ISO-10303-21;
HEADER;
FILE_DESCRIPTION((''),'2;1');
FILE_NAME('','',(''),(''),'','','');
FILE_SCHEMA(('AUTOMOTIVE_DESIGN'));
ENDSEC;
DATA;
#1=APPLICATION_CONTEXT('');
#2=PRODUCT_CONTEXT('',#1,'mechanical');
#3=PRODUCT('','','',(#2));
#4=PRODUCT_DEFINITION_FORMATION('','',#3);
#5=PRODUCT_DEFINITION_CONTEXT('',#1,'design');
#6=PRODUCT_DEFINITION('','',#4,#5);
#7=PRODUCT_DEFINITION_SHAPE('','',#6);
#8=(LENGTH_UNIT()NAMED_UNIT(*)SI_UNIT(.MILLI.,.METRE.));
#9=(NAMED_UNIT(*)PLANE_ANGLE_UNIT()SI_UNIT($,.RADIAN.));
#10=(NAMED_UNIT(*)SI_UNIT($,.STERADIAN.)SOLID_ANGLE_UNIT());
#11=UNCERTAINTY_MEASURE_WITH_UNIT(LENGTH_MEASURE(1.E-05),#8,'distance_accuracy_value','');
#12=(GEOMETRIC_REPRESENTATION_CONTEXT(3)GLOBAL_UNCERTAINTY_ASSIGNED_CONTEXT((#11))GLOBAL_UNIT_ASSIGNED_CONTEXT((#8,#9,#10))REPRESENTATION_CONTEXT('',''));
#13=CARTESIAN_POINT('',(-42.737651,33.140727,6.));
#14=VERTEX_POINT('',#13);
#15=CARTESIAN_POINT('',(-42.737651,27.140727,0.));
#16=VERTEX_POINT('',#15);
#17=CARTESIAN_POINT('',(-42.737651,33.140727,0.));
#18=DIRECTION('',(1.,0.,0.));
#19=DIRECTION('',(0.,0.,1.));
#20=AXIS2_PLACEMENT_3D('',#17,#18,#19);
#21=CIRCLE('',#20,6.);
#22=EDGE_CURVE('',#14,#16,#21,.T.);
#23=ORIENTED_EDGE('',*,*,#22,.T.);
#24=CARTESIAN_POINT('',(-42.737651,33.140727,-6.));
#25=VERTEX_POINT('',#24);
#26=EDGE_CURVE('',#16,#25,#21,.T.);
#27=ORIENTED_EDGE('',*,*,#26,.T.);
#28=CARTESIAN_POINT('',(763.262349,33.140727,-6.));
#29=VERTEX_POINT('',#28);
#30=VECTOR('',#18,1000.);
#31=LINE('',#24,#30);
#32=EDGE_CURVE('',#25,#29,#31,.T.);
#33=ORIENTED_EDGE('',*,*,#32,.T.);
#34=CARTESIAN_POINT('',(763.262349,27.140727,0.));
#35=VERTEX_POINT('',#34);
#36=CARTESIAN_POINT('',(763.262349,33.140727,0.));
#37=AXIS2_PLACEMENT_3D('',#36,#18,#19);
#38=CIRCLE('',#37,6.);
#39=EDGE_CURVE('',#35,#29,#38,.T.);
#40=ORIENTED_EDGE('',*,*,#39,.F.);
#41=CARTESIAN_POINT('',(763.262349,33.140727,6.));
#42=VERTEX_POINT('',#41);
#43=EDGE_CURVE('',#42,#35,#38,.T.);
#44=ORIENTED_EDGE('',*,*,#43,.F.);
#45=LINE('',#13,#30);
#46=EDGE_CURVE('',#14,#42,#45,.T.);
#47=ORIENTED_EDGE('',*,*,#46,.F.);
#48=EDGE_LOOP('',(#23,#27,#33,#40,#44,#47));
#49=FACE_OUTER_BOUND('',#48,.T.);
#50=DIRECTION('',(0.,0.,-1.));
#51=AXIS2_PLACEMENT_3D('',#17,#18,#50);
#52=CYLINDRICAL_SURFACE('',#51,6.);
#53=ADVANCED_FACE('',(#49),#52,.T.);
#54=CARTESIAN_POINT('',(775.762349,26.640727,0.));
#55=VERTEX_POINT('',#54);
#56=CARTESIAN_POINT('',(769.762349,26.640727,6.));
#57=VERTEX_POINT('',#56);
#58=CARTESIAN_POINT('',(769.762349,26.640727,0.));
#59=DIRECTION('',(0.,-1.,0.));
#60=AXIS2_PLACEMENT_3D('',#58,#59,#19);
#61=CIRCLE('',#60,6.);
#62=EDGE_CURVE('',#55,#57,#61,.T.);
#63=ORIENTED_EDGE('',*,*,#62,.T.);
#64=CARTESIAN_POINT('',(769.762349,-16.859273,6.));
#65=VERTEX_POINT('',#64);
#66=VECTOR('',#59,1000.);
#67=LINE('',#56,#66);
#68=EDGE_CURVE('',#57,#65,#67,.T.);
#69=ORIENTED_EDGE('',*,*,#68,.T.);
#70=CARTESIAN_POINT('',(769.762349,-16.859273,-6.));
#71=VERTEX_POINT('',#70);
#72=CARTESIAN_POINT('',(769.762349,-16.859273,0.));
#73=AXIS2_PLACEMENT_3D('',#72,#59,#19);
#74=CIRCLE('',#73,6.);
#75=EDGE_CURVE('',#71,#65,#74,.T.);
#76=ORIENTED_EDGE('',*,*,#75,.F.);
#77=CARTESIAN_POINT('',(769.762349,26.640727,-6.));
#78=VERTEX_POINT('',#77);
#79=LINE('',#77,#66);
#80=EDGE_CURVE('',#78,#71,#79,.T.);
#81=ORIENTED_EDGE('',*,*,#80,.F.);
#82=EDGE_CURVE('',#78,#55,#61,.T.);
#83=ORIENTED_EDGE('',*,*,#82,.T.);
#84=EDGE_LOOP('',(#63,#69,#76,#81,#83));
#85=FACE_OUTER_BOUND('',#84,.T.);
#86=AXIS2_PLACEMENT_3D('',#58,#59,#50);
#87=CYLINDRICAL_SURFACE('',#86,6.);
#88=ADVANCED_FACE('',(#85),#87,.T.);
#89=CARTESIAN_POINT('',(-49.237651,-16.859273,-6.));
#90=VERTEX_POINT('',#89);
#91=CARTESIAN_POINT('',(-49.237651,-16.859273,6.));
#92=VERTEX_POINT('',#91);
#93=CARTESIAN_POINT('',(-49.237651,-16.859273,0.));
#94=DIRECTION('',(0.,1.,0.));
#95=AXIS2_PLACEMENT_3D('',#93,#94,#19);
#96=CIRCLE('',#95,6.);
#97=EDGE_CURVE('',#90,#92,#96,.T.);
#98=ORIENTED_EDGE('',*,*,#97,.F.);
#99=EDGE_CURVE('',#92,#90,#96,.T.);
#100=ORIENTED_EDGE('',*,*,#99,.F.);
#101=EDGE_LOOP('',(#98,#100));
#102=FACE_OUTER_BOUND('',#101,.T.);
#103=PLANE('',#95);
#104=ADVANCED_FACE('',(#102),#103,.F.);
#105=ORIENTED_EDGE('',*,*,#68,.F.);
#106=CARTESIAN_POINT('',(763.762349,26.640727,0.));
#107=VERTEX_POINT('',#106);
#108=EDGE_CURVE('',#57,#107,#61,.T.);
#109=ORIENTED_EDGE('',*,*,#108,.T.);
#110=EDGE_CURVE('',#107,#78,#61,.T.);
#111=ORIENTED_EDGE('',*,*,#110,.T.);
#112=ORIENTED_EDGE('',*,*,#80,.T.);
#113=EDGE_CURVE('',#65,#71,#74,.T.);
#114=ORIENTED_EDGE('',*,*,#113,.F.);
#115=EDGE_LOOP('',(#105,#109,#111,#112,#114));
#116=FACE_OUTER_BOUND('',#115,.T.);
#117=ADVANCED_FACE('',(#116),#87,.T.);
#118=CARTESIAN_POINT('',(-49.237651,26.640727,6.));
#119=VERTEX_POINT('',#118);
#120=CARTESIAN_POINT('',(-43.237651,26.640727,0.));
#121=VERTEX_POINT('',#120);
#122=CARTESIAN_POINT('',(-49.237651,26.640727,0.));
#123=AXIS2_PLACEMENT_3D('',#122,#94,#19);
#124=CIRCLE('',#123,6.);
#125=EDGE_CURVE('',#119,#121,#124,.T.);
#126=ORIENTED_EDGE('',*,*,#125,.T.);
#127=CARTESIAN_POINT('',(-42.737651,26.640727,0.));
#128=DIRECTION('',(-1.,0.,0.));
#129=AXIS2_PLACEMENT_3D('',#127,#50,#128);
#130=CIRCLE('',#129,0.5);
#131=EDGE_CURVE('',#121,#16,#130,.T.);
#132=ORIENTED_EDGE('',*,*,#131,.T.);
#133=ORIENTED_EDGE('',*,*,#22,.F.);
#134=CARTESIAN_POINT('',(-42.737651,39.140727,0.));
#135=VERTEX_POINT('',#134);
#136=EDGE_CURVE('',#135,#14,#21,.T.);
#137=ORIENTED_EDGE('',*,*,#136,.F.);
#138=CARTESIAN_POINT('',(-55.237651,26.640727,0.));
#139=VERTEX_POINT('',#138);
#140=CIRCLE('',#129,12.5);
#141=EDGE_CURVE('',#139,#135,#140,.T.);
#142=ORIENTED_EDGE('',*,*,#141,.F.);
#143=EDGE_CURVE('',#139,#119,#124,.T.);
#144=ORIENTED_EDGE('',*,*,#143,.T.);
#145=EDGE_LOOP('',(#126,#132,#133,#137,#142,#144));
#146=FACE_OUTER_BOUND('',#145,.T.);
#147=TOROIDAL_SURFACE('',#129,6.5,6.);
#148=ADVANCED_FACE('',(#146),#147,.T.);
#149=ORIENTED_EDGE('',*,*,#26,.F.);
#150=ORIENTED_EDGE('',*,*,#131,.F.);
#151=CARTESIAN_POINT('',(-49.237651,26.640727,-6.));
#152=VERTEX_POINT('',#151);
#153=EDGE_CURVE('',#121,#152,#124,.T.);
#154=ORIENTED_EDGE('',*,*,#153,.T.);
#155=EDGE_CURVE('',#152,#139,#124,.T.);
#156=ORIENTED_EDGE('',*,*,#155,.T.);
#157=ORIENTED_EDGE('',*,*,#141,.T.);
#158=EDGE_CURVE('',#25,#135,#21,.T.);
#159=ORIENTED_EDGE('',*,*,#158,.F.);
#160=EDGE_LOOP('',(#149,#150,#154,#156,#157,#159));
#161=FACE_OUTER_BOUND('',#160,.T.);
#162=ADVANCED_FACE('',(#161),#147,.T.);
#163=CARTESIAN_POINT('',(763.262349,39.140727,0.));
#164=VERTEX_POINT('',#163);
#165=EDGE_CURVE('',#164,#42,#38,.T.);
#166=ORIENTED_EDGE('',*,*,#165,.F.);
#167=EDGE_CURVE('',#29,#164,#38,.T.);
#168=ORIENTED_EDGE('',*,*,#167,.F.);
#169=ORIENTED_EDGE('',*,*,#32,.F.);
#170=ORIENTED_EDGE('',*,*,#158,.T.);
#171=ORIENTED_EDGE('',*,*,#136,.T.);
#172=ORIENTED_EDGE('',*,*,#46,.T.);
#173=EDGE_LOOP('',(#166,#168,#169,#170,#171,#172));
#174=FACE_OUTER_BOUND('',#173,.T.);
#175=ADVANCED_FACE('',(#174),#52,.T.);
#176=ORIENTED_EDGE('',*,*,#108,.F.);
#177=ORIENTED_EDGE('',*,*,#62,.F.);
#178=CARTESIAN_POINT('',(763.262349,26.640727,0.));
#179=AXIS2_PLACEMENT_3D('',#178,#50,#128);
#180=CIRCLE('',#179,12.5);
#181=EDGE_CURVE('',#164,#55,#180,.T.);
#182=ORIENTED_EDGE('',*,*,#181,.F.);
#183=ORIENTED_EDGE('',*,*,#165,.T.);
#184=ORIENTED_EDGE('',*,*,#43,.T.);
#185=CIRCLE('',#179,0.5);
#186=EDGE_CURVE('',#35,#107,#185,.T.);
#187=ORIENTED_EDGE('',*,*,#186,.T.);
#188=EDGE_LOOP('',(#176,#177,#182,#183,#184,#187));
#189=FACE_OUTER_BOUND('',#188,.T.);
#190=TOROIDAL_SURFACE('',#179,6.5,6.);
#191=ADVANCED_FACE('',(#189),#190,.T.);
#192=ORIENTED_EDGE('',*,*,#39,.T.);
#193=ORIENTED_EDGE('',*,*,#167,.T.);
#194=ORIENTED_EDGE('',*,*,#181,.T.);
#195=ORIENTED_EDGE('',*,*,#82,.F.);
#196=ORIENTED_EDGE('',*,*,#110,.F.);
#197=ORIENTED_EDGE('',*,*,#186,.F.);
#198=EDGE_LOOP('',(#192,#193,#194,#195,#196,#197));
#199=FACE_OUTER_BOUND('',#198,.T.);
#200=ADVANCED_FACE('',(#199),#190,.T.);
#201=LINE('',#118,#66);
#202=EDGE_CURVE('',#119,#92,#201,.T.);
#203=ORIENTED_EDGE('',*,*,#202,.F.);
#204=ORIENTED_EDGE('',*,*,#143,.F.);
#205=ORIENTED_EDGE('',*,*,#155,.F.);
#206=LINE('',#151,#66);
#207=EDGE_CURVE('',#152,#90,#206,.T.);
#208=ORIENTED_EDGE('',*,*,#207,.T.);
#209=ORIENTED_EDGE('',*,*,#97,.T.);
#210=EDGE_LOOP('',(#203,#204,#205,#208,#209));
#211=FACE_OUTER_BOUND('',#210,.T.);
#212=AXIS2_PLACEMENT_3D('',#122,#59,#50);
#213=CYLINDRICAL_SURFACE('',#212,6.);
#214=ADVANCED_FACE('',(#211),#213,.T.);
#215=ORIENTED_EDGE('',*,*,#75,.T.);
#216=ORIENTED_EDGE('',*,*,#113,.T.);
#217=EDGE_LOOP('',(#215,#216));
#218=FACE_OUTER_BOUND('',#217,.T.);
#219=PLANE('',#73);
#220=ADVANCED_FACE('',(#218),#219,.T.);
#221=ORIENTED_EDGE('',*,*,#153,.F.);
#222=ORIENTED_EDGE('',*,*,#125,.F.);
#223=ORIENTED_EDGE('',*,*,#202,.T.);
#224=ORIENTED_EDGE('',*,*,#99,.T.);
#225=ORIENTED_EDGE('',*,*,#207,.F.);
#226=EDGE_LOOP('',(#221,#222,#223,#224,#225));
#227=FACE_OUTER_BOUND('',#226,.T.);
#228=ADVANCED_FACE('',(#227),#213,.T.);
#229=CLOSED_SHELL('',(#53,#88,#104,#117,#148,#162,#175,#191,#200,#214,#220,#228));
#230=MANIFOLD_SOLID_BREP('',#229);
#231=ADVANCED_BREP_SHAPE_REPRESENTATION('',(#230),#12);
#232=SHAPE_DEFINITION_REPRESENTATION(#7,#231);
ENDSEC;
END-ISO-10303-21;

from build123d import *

# Parameters (mm, degrees)
SKETCH2_R = 6


with BuildPart() as part:
    # Sweep1: sweep along a path in Sketch1
    with BuildLine(Plane.XY) as sweep1_path:
        Line((-49.237651445, -16.859273066), (-49.237651445, 26.640726934))
        ThreePointArc((-49.237651445, 26.640726934), (-47.333845522, 31.236921012), (-42.737651445, 33.140726934))
        Line((-42.737651445, 33.140726934), (763.262348555, 33.140726934))
        ThreePointArc((763.262348555, 33.140726934), (767.858542633, 31.236921012), (769.762348555, 26.640726934))
        Line((769.762348555, 26.640726934), (769.762348555, -16.859273066))
    # Sketch2 → Sweep1 (sweep)
    with BuildSketch(Plane(origin=(-49.237651445, -16.859273066, 0), x_dir=(-1, 0, 0), z_dir=(0, 1, 0))):
        Circle(SKETCH2_R)
    sweep(path=sweep1_path.line)


solid = part.part
